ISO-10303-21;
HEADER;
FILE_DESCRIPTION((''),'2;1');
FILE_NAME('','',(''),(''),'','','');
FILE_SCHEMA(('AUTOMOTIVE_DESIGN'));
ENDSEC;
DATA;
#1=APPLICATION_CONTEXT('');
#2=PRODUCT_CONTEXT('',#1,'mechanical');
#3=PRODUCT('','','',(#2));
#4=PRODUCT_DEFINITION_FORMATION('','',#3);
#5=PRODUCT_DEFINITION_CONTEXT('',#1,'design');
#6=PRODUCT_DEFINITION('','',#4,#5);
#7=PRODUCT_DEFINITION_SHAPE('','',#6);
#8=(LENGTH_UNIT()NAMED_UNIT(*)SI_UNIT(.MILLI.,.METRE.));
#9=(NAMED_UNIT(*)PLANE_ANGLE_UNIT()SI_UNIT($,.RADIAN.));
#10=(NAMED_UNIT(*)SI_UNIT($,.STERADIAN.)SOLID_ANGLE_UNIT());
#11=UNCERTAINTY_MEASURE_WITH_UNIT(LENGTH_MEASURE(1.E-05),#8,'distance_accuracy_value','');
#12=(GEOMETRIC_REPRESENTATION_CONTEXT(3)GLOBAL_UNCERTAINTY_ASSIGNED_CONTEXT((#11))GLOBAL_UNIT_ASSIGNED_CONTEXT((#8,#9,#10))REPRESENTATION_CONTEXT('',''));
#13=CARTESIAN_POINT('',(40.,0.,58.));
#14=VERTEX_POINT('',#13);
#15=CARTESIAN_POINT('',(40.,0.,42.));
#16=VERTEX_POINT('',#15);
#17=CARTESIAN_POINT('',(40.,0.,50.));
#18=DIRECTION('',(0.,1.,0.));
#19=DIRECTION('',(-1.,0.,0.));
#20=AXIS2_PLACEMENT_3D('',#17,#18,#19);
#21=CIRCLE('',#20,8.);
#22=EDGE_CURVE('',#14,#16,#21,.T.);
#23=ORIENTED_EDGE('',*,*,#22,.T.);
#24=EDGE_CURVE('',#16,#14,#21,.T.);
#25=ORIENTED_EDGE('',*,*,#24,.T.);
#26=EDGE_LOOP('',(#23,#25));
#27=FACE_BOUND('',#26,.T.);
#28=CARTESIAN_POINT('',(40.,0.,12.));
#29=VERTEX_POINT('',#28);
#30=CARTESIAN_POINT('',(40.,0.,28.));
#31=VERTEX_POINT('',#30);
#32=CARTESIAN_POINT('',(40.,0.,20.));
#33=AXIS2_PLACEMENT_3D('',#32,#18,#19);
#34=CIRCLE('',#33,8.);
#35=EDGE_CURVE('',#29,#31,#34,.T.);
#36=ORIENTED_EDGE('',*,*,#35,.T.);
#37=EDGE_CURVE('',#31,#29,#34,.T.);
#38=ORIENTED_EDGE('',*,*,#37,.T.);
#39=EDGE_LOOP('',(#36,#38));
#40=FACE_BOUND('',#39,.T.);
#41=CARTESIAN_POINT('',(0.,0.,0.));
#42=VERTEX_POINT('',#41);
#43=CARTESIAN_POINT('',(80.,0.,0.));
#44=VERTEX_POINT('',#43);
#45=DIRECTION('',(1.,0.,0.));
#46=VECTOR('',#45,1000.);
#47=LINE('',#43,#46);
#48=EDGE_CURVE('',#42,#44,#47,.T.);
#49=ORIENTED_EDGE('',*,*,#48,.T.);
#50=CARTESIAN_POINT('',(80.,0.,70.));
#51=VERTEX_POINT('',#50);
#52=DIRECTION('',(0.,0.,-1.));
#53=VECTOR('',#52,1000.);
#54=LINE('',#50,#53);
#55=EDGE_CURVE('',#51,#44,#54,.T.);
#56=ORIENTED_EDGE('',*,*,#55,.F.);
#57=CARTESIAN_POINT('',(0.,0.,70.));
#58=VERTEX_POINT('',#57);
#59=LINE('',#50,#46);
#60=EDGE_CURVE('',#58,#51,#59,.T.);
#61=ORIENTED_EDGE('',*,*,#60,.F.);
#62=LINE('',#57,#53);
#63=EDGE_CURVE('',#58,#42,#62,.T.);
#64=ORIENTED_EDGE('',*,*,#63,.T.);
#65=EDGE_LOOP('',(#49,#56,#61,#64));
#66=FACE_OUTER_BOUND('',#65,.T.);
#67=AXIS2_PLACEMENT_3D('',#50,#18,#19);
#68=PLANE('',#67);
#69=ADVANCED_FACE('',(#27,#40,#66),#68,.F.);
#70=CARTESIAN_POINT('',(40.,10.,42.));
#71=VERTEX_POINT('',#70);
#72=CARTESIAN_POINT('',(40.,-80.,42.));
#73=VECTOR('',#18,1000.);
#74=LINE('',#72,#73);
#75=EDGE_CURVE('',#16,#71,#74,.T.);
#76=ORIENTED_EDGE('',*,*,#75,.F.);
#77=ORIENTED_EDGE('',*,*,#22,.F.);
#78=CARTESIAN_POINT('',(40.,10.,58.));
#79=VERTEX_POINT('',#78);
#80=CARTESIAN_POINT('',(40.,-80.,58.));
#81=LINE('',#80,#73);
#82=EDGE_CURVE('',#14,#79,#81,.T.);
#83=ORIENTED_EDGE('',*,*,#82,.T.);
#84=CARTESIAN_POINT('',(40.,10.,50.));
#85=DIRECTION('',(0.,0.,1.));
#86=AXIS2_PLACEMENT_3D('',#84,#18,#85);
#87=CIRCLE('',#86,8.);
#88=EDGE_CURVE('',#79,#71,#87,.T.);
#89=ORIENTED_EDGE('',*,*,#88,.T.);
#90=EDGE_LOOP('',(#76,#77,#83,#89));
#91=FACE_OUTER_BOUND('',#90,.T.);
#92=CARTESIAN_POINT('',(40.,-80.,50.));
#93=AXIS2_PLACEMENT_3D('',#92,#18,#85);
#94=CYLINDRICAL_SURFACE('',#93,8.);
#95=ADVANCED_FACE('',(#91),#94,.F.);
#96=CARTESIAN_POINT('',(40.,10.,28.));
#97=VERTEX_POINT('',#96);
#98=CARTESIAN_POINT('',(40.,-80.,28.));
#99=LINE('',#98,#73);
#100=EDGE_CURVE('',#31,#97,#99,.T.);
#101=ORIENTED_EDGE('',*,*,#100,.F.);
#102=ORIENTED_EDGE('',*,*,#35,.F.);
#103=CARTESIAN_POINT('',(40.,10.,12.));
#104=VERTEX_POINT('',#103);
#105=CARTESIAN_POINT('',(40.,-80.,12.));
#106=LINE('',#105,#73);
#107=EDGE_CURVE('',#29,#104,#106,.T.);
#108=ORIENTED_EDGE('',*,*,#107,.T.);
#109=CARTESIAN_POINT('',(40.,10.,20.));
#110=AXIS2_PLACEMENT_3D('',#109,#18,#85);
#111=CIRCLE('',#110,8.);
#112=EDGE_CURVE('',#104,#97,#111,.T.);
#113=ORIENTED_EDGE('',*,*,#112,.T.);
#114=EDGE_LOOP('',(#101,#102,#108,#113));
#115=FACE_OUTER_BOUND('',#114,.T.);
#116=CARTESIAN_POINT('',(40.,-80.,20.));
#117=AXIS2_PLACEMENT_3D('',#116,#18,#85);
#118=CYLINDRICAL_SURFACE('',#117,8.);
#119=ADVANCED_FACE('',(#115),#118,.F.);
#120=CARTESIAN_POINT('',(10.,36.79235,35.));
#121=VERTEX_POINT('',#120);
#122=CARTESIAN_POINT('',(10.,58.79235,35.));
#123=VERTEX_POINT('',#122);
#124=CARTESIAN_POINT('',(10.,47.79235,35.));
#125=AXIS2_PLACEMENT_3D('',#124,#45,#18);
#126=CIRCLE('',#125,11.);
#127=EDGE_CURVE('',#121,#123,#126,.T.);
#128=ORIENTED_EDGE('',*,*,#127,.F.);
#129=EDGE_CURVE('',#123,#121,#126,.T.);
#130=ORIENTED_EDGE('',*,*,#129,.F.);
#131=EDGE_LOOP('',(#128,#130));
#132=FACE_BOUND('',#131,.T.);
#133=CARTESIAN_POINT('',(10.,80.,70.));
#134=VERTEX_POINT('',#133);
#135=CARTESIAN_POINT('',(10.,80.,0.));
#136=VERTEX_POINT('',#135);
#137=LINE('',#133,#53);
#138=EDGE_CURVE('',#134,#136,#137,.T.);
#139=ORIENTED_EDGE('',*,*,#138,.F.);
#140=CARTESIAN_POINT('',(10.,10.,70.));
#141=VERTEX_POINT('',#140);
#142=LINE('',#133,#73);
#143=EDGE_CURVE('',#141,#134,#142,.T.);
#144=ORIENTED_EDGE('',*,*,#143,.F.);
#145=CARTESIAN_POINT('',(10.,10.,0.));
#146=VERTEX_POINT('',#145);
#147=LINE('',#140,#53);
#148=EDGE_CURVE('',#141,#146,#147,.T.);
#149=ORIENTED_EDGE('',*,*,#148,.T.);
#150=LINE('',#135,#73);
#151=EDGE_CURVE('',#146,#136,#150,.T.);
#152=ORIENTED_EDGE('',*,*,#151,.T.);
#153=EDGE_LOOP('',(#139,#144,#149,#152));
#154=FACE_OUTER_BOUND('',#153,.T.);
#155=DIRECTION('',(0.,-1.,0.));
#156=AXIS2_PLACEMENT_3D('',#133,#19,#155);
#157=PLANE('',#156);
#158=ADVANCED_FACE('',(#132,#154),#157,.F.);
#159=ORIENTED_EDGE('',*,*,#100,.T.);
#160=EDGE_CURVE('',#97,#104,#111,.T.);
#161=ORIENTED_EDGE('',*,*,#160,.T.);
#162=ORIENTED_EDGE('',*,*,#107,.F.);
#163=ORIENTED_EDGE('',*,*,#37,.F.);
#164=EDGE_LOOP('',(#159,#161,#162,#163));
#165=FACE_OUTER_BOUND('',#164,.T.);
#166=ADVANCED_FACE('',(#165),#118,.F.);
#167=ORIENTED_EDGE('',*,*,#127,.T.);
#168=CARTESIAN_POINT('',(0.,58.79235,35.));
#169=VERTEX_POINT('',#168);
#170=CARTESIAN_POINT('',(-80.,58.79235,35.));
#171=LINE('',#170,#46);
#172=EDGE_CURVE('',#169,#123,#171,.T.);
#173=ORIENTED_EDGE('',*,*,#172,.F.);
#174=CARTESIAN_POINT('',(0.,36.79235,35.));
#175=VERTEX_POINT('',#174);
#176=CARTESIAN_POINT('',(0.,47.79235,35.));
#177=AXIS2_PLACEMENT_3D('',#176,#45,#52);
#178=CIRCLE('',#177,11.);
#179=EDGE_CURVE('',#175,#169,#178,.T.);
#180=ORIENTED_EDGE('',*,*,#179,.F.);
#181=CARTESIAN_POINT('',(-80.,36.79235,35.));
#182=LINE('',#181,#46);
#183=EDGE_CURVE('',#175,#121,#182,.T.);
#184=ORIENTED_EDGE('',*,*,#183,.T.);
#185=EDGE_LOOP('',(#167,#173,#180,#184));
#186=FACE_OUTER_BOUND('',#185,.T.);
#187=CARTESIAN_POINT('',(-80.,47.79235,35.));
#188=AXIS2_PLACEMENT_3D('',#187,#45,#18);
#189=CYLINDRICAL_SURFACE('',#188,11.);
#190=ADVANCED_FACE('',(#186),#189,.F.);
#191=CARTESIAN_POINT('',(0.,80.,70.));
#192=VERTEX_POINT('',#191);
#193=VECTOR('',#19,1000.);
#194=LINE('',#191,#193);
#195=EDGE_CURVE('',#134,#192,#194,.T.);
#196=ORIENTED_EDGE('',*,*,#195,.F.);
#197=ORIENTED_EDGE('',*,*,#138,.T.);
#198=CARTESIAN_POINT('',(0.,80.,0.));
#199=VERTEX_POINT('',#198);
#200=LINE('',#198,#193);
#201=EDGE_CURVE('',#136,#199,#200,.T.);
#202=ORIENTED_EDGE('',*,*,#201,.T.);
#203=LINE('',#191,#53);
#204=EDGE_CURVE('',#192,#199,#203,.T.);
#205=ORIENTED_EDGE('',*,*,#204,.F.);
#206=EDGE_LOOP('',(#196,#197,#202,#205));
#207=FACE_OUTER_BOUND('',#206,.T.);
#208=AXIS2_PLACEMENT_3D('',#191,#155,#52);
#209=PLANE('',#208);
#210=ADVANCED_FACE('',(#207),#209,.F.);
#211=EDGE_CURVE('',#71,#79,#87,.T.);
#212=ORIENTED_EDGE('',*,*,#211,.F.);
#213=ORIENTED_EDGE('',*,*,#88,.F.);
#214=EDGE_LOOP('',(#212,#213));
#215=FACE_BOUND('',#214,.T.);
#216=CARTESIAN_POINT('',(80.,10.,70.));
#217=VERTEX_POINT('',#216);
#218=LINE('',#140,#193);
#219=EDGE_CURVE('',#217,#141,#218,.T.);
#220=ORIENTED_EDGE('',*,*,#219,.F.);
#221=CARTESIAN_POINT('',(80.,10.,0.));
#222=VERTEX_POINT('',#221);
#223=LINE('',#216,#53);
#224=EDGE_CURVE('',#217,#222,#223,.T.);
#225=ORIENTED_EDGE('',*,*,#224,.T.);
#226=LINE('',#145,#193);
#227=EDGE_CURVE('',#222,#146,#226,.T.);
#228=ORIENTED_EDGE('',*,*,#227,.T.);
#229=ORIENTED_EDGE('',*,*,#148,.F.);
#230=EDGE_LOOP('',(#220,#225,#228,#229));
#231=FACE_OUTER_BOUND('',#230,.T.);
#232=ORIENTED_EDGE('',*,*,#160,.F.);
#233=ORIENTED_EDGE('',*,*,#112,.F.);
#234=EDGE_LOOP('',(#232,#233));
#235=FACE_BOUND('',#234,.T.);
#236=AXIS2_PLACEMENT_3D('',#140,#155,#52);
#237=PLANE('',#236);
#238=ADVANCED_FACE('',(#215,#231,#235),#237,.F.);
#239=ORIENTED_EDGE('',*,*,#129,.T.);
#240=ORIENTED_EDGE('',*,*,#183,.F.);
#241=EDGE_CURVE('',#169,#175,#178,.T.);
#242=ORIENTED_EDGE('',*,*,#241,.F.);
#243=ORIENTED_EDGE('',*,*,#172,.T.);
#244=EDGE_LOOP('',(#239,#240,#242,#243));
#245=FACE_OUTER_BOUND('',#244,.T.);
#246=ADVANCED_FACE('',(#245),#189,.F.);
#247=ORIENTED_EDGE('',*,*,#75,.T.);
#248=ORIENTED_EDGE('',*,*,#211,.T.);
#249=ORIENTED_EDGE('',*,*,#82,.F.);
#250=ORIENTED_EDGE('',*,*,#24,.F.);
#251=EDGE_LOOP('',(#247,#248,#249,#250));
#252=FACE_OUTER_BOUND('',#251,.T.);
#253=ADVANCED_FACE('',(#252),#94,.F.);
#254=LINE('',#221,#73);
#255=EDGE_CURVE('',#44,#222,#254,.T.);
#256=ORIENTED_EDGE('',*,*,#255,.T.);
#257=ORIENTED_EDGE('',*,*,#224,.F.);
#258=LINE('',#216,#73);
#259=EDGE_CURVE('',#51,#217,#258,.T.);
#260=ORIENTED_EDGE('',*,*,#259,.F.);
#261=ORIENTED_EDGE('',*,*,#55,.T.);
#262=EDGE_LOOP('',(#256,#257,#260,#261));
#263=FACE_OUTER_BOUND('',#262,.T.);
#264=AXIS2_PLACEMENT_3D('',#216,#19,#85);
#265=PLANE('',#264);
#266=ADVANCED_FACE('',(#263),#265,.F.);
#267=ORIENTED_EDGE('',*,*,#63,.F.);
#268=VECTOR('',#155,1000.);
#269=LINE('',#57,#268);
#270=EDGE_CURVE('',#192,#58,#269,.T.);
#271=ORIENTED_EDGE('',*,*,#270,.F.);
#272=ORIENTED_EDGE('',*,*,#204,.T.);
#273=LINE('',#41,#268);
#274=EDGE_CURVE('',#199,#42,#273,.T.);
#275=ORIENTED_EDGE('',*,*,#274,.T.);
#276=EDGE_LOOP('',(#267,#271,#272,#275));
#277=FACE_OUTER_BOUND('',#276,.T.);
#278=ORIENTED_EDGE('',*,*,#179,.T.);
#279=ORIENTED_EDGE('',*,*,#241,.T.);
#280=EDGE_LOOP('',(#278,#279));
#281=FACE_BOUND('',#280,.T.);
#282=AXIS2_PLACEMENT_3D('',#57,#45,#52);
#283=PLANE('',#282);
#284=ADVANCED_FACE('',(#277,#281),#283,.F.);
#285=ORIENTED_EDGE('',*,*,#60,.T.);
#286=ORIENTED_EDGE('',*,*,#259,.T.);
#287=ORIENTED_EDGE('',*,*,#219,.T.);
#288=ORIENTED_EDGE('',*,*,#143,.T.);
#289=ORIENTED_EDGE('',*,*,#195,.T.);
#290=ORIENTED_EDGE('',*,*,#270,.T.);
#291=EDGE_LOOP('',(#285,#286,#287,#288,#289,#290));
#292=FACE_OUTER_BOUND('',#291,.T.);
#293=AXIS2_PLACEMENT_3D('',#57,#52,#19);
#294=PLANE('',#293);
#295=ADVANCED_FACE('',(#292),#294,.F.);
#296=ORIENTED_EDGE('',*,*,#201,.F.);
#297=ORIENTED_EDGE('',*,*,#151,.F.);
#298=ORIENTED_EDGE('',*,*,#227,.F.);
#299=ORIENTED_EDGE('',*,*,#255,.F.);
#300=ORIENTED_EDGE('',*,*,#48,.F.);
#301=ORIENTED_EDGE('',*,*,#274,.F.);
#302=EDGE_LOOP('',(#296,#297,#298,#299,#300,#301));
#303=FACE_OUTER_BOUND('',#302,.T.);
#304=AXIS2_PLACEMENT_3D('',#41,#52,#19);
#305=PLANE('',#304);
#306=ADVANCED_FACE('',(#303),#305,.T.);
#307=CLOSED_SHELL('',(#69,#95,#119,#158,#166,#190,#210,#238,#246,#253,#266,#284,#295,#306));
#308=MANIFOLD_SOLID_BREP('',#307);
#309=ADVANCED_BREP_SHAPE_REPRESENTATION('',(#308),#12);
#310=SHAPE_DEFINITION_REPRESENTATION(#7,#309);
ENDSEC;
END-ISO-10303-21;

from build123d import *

# Parameters (mm, degrees)
BOSS_EXTRUDE1_DEPTH = 70
SKETCH2_R           = 8
CUT_EXTRUDE1_DEPTH  = 90
SKETCH3_R           = 11
CUT_EXTRUDE2_DEPTH  = 90


with BuildPart() as part:
    # Sketch1 → Boss-Extrude1 (new body)
    with BuildSketch(Plane.XY):
        Polygon((0, 0), (0, 80), (10, 80), (10, 10), (80, 10), (80, 0), align=None)
    extrude(amount=BOSS_EXTRUDE1_DEPTH)

    # Sketch2 → Cut-Extrude1 (cut)
    with BuildSketch(Plane(origin=(0, 10, 0), x_dir=(1, 0, 0), z_dir=(0, 1, 0))):
        with Locations(Location((40, -20, 0), (0, 0, 270))):
            Circle(SKETCH2_R)
        with Locations(Location((40, -50, 0), (0, 0, 270))):
            Circle(SKETCH2_R)
    extrude(amount=-CUT_EXTRUDE1_DEPTH, mode=Mode.SUBTRACT)

    # Sketch3 → Cut-Extrude2 (cut)
    with BuildSketch(Plane(origin=(10, 0, 0), x_dir=(0, 0, -1), z_dir=(1, 0, 0))):
        with Locations(Location((-35, 47.792350155, 0), (0, 0, 90))):
            Circle(SKETCH3_R)
    extrude(amount=-CUT_EXTRUDE2_DEPTH, mode=Mode.SUBTRACT)


solid = part.part
